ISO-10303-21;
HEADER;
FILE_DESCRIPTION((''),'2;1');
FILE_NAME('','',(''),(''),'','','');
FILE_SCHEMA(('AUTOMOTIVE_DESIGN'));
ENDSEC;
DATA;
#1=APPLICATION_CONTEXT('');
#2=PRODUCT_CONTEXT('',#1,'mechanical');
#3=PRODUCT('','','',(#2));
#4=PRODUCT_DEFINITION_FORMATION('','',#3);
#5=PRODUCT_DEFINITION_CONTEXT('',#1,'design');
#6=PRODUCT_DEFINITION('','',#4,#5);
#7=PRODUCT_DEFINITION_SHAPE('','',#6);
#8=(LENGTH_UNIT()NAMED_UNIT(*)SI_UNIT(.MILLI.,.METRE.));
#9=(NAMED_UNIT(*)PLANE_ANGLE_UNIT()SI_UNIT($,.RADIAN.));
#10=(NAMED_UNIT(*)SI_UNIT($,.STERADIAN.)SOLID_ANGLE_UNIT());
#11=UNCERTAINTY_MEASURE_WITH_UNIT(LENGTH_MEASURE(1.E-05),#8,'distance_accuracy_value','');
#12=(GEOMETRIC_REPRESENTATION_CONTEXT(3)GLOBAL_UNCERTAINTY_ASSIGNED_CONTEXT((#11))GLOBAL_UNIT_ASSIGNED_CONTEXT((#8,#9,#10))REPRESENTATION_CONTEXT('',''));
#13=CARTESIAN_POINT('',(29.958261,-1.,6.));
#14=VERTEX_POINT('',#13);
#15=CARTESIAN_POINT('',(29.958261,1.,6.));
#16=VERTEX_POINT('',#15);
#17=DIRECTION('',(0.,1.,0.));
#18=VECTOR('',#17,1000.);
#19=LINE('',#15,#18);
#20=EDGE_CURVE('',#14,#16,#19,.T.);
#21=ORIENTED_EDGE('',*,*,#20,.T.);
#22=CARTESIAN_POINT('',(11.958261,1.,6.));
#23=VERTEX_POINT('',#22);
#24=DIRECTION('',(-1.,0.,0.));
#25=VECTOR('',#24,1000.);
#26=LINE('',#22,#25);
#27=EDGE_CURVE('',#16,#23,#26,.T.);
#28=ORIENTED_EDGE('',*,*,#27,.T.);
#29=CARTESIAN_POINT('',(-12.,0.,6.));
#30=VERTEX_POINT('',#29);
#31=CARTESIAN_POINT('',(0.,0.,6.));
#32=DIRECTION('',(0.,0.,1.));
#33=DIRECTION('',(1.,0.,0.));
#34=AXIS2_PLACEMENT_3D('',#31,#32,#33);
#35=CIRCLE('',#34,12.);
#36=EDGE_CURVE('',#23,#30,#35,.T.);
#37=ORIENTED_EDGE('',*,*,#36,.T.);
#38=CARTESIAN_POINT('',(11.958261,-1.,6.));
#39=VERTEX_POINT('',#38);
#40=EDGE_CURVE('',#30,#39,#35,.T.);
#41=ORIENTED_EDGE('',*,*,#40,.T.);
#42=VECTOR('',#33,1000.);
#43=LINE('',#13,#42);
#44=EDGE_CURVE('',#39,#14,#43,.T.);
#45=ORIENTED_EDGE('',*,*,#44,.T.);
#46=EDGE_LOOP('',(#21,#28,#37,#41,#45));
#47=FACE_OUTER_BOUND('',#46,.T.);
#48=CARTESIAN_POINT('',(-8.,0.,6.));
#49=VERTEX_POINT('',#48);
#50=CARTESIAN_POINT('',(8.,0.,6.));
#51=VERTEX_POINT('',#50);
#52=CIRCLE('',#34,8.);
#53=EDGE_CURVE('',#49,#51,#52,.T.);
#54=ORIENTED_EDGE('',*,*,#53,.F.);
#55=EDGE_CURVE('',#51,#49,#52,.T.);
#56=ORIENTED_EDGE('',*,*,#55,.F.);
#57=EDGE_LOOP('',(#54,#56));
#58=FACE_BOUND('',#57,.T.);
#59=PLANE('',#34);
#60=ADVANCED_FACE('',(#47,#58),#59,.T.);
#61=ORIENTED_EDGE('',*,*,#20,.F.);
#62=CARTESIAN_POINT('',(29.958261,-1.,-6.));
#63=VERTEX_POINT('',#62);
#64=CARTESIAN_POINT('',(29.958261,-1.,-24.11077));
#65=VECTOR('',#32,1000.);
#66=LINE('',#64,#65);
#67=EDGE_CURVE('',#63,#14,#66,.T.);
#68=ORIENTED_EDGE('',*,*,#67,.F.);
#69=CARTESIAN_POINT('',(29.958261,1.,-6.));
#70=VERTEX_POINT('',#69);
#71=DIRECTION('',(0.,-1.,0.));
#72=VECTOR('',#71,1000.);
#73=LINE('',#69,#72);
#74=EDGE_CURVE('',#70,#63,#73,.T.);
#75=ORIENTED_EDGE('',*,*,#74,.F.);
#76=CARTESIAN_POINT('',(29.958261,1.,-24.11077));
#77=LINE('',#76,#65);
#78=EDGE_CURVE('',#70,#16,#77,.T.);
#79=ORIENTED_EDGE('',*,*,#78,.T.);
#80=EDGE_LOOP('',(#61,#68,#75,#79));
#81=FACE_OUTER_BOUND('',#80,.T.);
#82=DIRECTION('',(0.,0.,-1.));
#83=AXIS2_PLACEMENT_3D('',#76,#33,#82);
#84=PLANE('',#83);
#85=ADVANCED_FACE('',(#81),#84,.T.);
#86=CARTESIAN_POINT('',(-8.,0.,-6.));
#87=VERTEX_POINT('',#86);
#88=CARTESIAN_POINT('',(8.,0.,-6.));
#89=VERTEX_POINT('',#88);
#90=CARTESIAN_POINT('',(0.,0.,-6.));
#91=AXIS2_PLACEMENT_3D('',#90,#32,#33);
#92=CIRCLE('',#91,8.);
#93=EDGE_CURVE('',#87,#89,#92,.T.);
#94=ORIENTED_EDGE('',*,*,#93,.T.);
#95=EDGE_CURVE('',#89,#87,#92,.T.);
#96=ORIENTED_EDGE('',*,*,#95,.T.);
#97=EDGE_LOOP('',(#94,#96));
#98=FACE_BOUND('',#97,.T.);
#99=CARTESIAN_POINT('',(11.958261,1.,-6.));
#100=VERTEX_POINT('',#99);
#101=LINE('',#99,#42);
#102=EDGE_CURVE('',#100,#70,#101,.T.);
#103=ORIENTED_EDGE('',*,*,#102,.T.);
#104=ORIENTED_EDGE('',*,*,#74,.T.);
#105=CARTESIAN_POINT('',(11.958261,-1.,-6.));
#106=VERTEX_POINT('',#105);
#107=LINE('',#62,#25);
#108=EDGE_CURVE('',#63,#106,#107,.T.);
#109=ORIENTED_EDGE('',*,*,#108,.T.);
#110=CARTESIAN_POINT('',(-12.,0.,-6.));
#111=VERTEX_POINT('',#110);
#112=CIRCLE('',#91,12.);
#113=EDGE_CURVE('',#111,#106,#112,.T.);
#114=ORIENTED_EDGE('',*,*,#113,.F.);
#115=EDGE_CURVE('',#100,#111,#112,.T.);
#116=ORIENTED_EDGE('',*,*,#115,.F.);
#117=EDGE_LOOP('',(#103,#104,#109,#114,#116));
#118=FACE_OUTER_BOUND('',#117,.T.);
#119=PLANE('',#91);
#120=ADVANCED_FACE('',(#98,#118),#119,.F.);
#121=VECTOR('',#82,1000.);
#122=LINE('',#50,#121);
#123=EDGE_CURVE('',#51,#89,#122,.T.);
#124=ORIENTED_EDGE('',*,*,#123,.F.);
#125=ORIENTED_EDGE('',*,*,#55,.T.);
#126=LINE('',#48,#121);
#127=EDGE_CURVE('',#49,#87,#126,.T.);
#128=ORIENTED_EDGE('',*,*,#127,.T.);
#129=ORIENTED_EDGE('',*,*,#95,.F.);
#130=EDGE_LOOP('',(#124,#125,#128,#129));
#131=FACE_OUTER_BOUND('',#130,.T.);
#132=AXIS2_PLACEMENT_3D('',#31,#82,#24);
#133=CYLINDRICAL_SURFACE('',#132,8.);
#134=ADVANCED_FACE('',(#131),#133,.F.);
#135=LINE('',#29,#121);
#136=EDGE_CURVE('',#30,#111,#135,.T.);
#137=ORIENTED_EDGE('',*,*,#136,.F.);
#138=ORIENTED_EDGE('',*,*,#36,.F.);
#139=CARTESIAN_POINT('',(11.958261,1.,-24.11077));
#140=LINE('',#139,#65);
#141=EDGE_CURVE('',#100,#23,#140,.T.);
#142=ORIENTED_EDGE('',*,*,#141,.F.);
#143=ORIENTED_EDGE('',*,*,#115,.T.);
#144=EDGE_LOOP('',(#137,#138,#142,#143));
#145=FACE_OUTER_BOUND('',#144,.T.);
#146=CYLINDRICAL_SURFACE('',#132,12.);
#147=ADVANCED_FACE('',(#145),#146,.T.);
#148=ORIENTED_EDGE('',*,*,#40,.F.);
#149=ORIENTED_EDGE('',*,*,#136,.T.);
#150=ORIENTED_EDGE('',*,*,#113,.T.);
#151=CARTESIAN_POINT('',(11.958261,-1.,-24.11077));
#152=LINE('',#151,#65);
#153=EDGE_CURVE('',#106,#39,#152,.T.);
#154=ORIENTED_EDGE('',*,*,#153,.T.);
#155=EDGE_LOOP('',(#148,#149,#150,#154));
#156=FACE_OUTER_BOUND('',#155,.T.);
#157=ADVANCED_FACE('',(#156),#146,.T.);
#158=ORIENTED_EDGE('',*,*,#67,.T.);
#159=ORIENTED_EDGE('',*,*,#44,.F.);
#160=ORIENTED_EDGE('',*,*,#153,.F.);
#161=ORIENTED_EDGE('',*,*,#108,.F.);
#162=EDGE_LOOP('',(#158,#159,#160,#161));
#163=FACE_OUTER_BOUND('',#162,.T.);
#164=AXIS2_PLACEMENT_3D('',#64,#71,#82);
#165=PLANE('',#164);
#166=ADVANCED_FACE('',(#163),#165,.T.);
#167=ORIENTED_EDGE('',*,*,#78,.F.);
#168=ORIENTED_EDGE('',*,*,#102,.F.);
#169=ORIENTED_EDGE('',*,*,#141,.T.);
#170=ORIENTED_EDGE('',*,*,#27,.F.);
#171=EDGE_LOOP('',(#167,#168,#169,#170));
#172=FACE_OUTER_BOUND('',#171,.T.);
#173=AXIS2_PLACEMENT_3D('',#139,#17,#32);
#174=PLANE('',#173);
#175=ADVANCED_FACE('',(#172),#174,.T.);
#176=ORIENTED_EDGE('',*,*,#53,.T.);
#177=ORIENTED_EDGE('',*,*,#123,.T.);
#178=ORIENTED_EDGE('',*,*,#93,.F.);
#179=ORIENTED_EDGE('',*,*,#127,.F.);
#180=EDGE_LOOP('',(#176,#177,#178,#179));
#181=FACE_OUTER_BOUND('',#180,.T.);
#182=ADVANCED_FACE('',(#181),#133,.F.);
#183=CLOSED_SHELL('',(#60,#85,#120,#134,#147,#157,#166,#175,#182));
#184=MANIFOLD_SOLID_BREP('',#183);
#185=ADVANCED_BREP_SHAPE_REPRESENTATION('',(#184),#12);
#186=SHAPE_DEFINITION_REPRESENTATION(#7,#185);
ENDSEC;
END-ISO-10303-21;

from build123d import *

# Parameters (mm, degrees)
SKETCH_1_R      = 12
SKETCH_1_R_2    = 8
EXTRUDE_1_DEPTH = 6
SKETCH_2_W      = 18
SKETCH_2_H      = 2
EXTRUDE_2_DEPTH = 12


with BuildPart() as part:
    # 草图1 → 凸台-拉伸1 (new, symmetric)
    with BuildSketch(Plane.XY):
        Circle(SKETCH_1_R)
        Circle(SKETCH_1_R_2, mode=Mode.SUBTRACT)
    extrude(amount=EXTRUDE_1_DEPTH, both=True)

    # 草图2 → 凸台-拉伸2 (add)
    with BuildSketch(Plane.XY.offset(6)):
        with Locations((20.958260743, 0)):
            Rectangle(SKETCH_2_W, SKETCH_2_H)
    extrude(amount=-EXTRUDE_2_DEPTH)


solid = part.part
